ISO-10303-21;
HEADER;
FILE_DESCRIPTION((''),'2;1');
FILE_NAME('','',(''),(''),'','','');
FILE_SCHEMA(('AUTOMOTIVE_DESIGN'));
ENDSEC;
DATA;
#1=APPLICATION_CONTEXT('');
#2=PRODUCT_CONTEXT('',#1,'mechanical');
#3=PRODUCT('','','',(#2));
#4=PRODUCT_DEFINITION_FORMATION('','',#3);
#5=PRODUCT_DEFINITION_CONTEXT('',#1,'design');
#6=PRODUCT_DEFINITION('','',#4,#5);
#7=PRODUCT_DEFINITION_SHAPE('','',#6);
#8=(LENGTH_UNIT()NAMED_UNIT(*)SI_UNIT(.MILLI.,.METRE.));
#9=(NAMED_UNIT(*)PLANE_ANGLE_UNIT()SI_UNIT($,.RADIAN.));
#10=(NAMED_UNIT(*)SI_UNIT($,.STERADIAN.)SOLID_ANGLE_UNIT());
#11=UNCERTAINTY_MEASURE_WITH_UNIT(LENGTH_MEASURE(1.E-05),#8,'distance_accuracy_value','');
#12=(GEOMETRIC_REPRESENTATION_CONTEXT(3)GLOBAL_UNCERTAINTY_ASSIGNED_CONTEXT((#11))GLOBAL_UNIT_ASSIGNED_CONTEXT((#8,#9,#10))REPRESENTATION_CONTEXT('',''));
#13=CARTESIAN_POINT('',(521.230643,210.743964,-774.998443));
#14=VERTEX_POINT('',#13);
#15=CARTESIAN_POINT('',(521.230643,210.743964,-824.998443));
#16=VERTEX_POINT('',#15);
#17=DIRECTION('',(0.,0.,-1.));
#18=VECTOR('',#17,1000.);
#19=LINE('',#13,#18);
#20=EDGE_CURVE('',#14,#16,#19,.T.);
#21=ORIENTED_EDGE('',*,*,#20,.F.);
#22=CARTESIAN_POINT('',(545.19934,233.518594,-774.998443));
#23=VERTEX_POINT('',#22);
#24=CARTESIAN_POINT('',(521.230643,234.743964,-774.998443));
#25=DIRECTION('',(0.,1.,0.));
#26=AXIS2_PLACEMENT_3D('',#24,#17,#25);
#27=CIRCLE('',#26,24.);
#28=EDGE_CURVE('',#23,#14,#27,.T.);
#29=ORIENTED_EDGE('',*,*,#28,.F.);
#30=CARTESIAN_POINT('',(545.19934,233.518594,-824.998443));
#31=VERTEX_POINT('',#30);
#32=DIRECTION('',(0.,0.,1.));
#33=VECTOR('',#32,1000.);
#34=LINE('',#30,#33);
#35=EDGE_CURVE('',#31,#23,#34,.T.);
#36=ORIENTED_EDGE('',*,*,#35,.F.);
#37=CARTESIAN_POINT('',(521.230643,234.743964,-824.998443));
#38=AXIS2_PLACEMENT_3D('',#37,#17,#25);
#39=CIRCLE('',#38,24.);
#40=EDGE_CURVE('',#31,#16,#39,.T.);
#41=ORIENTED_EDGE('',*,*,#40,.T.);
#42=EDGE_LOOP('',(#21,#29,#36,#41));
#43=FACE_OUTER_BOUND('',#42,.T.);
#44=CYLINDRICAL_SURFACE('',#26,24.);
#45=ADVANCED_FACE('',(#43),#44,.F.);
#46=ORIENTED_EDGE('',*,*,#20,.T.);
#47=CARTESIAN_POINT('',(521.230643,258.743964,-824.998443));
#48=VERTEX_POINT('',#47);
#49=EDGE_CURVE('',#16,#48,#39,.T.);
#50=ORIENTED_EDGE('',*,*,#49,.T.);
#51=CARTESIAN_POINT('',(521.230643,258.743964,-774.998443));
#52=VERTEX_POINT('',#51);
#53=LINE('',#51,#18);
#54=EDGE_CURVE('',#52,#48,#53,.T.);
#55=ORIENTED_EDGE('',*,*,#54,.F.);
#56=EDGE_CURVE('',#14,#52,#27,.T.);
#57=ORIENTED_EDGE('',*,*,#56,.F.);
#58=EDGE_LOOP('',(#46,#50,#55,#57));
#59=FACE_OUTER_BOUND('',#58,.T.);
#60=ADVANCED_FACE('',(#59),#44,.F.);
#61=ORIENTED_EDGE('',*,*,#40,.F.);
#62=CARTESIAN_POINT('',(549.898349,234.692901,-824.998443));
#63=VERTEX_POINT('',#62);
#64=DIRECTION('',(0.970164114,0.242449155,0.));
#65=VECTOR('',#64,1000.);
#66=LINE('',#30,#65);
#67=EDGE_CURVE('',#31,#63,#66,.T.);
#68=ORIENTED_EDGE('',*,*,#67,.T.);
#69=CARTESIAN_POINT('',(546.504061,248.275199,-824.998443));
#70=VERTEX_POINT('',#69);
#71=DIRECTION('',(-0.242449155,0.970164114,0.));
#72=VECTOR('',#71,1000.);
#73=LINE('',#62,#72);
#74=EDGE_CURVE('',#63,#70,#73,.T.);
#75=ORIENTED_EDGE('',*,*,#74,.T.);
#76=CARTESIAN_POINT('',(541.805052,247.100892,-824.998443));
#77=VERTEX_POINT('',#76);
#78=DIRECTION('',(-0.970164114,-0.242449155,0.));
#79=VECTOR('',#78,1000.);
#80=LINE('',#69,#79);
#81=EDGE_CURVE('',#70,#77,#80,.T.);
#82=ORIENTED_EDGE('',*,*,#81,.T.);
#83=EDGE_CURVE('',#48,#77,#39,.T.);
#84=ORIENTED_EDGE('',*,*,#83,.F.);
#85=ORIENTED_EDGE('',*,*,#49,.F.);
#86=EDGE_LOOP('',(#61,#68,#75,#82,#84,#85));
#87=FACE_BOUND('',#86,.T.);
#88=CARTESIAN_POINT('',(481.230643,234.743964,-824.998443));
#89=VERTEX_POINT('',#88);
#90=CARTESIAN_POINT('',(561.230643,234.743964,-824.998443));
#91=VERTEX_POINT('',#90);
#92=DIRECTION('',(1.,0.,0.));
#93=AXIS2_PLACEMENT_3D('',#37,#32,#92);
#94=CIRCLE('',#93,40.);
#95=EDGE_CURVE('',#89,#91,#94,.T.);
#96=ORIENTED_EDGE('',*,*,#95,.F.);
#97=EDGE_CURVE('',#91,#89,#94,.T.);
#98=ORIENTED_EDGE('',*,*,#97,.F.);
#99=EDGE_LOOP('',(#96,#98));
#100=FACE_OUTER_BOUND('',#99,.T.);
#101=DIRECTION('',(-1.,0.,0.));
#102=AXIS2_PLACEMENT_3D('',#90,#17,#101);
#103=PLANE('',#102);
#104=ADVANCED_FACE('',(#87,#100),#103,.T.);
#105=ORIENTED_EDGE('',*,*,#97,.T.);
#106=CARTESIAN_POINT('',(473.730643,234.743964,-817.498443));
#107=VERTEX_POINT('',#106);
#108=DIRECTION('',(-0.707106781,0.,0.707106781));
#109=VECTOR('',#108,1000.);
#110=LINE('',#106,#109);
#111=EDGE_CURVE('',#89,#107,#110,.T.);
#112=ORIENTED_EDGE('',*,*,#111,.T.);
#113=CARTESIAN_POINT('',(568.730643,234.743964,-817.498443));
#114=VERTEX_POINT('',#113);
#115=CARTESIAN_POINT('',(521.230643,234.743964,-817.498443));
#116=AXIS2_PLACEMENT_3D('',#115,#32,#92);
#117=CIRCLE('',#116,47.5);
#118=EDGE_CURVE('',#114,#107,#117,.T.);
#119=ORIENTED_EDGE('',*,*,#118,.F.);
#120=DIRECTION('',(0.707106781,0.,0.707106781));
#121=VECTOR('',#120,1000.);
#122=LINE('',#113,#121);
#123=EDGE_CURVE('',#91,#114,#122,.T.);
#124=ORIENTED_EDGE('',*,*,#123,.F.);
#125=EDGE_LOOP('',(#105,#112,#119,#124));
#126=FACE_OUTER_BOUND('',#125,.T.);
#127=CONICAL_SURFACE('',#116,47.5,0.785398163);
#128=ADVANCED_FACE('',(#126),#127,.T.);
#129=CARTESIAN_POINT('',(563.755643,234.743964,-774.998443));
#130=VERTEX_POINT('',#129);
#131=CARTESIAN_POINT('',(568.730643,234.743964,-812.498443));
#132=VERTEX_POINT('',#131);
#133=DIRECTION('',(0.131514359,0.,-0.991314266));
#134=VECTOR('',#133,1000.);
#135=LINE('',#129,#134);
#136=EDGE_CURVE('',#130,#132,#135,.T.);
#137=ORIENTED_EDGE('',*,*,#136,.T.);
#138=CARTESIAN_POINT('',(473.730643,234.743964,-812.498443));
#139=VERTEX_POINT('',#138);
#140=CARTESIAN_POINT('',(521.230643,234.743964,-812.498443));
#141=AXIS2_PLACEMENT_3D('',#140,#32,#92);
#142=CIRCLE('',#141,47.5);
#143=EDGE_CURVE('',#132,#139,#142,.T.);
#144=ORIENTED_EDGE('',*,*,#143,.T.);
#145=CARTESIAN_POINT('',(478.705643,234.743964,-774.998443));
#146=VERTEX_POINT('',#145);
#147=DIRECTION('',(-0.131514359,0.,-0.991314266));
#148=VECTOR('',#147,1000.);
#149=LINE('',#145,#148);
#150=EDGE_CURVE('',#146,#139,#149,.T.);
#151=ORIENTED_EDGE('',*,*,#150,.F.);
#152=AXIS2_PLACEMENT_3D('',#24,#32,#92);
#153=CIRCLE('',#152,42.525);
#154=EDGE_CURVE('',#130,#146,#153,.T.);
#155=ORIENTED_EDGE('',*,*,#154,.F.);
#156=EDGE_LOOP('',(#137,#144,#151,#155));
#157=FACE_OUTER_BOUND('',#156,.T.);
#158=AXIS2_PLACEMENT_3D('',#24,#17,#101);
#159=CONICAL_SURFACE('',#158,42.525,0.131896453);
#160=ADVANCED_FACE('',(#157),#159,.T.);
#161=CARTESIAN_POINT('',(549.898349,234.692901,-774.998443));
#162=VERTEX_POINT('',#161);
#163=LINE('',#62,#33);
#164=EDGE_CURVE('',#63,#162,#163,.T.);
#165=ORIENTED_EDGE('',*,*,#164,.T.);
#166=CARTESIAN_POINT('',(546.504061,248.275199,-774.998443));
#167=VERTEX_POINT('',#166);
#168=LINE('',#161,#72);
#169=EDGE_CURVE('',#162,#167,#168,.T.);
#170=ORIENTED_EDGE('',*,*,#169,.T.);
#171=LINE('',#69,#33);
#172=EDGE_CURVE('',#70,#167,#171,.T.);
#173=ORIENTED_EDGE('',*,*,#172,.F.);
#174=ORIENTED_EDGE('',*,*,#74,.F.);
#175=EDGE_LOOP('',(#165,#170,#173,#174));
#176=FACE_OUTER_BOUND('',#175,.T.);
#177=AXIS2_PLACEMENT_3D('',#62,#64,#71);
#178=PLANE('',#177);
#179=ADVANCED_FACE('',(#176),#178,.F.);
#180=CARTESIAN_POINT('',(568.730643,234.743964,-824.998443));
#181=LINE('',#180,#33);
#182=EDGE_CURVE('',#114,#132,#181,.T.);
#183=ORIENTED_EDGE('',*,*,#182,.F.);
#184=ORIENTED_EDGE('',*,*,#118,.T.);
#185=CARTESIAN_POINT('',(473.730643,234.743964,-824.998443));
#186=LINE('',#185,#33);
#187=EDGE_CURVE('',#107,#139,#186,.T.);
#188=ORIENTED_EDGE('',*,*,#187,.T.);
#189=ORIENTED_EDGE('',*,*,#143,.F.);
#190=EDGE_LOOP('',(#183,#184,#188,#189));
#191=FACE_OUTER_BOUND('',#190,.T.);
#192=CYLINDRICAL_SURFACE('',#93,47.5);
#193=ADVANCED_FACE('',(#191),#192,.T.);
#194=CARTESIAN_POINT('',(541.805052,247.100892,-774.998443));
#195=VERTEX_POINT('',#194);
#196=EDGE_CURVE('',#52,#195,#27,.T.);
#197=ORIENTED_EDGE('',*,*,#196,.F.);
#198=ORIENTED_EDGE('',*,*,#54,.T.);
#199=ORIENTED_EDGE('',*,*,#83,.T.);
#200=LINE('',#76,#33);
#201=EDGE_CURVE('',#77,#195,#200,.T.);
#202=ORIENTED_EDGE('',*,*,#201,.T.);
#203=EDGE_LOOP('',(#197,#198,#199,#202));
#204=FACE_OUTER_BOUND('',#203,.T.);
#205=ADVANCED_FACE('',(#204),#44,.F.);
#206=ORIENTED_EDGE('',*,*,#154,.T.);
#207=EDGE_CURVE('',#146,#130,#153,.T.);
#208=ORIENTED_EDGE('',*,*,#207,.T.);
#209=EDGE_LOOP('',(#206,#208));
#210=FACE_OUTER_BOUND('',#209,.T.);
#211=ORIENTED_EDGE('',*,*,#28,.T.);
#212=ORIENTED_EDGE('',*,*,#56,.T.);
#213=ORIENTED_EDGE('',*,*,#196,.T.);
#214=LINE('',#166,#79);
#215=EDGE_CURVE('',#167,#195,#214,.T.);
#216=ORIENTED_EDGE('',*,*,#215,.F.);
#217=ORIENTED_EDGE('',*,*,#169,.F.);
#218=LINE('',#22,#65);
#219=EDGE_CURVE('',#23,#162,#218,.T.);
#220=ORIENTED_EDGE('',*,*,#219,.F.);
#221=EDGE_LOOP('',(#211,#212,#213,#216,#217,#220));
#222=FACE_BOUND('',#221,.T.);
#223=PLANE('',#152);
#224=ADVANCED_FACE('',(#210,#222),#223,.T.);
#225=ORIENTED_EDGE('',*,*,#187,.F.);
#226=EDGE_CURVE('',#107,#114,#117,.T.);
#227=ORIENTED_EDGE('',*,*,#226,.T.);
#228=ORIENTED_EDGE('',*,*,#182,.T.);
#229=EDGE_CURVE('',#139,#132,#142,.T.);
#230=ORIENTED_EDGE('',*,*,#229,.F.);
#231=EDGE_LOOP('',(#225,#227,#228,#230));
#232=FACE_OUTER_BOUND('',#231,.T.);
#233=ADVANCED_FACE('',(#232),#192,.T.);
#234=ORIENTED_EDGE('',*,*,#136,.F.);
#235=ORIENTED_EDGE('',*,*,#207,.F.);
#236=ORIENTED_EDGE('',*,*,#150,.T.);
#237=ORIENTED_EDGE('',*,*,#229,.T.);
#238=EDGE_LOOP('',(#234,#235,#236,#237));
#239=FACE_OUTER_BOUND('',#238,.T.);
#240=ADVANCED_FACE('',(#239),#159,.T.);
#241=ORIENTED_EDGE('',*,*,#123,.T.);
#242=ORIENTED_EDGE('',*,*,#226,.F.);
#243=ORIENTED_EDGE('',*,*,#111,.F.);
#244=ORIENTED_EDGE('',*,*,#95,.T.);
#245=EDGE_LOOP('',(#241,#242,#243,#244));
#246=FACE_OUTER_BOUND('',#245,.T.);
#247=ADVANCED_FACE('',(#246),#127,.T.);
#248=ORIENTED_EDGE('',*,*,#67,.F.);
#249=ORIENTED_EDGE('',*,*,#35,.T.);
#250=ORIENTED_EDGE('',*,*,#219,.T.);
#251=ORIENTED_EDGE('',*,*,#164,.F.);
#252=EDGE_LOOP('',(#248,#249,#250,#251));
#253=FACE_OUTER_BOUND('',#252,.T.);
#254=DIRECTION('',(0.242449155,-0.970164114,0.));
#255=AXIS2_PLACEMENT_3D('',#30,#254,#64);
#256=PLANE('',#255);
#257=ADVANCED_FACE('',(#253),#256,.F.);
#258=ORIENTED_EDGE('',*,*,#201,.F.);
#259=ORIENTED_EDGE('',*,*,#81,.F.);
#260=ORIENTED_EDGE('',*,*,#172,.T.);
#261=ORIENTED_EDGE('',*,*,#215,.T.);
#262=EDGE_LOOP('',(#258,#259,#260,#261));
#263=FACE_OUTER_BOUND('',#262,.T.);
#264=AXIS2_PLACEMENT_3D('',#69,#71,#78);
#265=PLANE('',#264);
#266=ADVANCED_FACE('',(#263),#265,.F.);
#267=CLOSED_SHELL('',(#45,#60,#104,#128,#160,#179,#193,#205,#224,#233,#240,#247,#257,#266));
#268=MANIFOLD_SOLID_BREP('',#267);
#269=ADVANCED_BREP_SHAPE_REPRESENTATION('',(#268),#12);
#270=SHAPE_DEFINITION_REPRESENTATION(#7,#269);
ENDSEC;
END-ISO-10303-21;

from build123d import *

# Parameters (mm, degrees)
CUT_EXTRUDE1_DEPTH = 637.880050586
SKETCH3_W          = 24
SKETCH3_H          = 50


with BuildPart() as part:
    # Sketch1 → Revolve1 (revolve)
    with BuildSketch(Plane(origin=(0, 234.743963655, 0), x_dir=(1, 0, 0), z_dir=(0, 1, 0))):
        Polygon((561.230642584, 824.998443067), (521.230642584, 824.998443067), (521.230642584, 774.998443067), (563.755642584, 774.998443067), (568.730642584, 812.498443067), (568.730642584, 817.498443067), align=None)
    revolve(axis=Axis((521.230642584, 234.743963655, -824.998443067), (0, 0, 1)))

    # Sketch2 → Cut-Extrude1 (cut, through all)
    with BuildSketch(Plane.XY.offset(-774.998443067)):
        with BuildLine():
            Line((549.898349026, 234.692901362), (546.50406086, 248.275198952))
            Line((546.50406086, 248.275198952), (541.805052122, 247.10089176))
            ThreePointArc((541.805052122, 247.10089176), (544.514581311, 240.562743369), (545.199340288, 233.518594169))
            Line((545.199340288, 233.518594169), (549.898349026, 234.692901362))
        make_face()
    extrude(amount=-CUT_EXTRUDE1_DEPTH, mode=Mode.SUBTRACT)

    # Sketch3 → Cut-Revolve1 (revolve, cut)
    with BuildSketch(Plane.XZ.offset(-234.743963655)):
        with Locations((533.230642584, -799.998443067)):
            Rectangle(SKETCH3_W, SKETCH3_H)
    revolve(axis=Axis((521.230642584, 234.743963655, -774.998443067), (0, 0, -1)), mode=Mode.SUBTRACT)


solid = part.part
